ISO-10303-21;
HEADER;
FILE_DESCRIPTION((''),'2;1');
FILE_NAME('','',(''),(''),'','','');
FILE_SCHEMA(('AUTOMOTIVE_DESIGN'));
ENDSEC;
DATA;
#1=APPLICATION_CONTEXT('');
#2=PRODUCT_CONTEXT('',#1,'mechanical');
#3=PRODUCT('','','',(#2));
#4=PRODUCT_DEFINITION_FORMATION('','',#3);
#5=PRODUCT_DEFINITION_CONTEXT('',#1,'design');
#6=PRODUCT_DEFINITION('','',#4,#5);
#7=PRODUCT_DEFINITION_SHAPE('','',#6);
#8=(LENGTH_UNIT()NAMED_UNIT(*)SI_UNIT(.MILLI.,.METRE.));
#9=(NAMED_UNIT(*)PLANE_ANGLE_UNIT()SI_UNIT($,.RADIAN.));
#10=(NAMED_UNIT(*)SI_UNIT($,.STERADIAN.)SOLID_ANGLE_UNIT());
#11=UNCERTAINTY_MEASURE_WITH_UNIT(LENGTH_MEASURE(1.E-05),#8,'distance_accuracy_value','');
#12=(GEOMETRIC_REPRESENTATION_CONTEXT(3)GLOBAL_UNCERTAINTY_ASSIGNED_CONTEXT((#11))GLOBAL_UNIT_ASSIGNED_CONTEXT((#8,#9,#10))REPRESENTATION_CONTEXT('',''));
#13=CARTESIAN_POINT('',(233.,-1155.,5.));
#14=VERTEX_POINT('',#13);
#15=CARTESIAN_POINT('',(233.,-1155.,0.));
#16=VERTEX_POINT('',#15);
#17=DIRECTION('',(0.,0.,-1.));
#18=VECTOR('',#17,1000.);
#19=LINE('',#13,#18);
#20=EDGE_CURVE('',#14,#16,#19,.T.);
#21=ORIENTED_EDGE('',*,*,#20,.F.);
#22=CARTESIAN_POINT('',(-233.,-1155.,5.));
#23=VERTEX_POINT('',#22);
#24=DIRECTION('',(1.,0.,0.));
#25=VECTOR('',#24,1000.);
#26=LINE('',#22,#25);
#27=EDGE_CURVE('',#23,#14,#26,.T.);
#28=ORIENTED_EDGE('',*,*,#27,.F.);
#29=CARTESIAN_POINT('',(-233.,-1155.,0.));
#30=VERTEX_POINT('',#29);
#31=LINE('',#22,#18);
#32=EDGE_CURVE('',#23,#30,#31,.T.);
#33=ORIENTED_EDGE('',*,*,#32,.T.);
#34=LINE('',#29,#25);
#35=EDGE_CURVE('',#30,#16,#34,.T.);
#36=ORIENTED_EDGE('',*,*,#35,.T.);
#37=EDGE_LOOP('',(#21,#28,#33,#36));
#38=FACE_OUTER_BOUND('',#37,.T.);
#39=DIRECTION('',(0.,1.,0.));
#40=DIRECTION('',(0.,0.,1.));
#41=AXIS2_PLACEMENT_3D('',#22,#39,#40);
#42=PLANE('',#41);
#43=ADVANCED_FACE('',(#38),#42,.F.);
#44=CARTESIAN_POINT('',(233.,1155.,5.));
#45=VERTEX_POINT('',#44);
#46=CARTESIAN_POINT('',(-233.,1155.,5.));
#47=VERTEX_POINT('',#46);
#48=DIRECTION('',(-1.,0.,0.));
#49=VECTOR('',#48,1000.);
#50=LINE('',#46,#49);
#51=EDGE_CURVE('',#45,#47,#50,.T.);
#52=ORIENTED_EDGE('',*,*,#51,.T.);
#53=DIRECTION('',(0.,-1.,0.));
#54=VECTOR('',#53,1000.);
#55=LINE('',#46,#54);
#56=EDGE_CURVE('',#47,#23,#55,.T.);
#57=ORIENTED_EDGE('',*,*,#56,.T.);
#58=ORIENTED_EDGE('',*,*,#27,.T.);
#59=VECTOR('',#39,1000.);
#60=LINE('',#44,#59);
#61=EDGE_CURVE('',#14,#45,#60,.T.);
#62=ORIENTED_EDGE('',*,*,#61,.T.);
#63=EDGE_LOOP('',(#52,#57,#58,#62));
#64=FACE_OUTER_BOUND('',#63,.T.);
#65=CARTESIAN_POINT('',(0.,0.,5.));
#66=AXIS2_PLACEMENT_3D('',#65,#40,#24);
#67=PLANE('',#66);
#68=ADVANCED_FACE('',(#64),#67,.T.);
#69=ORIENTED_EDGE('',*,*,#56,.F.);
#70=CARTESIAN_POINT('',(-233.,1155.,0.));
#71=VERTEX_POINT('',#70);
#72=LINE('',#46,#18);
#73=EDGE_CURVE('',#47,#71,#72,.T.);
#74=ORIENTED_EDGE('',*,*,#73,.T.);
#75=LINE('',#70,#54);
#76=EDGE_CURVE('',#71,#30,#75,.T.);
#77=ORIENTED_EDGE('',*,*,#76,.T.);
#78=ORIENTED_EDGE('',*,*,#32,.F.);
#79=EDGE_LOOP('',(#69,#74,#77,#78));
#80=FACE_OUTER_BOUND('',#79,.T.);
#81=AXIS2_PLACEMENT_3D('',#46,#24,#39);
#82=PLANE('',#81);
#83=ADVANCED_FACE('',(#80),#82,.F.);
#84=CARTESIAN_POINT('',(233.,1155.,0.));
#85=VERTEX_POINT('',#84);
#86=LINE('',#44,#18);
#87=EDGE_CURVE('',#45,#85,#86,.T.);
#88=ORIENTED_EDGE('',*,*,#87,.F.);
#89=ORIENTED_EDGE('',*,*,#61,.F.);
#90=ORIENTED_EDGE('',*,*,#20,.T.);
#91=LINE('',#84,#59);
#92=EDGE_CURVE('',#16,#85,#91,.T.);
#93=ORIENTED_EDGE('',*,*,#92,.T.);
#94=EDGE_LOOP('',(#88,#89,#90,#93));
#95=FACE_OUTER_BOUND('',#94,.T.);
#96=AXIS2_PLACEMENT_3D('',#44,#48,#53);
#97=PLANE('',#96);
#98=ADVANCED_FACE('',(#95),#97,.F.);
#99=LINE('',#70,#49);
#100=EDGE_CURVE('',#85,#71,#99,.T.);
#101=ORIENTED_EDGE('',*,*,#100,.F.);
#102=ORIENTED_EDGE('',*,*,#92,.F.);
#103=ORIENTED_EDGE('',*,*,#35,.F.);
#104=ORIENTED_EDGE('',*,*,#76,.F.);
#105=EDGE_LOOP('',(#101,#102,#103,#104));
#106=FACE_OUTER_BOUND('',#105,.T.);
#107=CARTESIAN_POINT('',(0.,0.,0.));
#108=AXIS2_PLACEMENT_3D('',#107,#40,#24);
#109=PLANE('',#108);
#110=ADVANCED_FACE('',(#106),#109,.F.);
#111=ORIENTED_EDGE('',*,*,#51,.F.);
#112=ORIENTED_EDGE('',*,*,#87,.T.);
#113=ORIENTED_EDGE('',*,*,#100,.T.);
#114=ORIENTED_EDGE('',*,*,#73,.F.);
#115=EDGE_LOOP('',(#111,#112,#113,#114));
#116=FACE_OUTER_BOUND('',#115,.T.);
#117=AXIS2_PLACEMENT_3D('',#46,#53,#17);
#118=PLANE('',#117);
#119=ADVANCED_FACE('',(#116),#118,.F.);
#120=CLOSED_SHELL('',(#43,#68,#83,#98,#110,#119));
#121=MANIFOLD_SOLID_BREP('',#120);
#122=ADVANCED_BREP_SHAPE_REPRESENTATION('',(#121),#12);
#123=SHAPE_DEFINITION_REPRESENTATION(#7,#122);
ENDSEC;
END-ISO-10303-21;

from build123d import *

# Parameters (mm, degrees)
SKETCH_1_W      = 466
SKETCH_1_H      = 2310
EXTRUDE_1_DEPTH = 5


with BuildPart() as part:
    # 草图1 → 凸台-拉伸1 (new body)
    with BuildSketch(Plane.XY):
        Rectangle(SKETCH_1_W, SKETCH_1_H)
    extrude(amount=EXTRUDE_1_DEPTH)


solid = part.part
